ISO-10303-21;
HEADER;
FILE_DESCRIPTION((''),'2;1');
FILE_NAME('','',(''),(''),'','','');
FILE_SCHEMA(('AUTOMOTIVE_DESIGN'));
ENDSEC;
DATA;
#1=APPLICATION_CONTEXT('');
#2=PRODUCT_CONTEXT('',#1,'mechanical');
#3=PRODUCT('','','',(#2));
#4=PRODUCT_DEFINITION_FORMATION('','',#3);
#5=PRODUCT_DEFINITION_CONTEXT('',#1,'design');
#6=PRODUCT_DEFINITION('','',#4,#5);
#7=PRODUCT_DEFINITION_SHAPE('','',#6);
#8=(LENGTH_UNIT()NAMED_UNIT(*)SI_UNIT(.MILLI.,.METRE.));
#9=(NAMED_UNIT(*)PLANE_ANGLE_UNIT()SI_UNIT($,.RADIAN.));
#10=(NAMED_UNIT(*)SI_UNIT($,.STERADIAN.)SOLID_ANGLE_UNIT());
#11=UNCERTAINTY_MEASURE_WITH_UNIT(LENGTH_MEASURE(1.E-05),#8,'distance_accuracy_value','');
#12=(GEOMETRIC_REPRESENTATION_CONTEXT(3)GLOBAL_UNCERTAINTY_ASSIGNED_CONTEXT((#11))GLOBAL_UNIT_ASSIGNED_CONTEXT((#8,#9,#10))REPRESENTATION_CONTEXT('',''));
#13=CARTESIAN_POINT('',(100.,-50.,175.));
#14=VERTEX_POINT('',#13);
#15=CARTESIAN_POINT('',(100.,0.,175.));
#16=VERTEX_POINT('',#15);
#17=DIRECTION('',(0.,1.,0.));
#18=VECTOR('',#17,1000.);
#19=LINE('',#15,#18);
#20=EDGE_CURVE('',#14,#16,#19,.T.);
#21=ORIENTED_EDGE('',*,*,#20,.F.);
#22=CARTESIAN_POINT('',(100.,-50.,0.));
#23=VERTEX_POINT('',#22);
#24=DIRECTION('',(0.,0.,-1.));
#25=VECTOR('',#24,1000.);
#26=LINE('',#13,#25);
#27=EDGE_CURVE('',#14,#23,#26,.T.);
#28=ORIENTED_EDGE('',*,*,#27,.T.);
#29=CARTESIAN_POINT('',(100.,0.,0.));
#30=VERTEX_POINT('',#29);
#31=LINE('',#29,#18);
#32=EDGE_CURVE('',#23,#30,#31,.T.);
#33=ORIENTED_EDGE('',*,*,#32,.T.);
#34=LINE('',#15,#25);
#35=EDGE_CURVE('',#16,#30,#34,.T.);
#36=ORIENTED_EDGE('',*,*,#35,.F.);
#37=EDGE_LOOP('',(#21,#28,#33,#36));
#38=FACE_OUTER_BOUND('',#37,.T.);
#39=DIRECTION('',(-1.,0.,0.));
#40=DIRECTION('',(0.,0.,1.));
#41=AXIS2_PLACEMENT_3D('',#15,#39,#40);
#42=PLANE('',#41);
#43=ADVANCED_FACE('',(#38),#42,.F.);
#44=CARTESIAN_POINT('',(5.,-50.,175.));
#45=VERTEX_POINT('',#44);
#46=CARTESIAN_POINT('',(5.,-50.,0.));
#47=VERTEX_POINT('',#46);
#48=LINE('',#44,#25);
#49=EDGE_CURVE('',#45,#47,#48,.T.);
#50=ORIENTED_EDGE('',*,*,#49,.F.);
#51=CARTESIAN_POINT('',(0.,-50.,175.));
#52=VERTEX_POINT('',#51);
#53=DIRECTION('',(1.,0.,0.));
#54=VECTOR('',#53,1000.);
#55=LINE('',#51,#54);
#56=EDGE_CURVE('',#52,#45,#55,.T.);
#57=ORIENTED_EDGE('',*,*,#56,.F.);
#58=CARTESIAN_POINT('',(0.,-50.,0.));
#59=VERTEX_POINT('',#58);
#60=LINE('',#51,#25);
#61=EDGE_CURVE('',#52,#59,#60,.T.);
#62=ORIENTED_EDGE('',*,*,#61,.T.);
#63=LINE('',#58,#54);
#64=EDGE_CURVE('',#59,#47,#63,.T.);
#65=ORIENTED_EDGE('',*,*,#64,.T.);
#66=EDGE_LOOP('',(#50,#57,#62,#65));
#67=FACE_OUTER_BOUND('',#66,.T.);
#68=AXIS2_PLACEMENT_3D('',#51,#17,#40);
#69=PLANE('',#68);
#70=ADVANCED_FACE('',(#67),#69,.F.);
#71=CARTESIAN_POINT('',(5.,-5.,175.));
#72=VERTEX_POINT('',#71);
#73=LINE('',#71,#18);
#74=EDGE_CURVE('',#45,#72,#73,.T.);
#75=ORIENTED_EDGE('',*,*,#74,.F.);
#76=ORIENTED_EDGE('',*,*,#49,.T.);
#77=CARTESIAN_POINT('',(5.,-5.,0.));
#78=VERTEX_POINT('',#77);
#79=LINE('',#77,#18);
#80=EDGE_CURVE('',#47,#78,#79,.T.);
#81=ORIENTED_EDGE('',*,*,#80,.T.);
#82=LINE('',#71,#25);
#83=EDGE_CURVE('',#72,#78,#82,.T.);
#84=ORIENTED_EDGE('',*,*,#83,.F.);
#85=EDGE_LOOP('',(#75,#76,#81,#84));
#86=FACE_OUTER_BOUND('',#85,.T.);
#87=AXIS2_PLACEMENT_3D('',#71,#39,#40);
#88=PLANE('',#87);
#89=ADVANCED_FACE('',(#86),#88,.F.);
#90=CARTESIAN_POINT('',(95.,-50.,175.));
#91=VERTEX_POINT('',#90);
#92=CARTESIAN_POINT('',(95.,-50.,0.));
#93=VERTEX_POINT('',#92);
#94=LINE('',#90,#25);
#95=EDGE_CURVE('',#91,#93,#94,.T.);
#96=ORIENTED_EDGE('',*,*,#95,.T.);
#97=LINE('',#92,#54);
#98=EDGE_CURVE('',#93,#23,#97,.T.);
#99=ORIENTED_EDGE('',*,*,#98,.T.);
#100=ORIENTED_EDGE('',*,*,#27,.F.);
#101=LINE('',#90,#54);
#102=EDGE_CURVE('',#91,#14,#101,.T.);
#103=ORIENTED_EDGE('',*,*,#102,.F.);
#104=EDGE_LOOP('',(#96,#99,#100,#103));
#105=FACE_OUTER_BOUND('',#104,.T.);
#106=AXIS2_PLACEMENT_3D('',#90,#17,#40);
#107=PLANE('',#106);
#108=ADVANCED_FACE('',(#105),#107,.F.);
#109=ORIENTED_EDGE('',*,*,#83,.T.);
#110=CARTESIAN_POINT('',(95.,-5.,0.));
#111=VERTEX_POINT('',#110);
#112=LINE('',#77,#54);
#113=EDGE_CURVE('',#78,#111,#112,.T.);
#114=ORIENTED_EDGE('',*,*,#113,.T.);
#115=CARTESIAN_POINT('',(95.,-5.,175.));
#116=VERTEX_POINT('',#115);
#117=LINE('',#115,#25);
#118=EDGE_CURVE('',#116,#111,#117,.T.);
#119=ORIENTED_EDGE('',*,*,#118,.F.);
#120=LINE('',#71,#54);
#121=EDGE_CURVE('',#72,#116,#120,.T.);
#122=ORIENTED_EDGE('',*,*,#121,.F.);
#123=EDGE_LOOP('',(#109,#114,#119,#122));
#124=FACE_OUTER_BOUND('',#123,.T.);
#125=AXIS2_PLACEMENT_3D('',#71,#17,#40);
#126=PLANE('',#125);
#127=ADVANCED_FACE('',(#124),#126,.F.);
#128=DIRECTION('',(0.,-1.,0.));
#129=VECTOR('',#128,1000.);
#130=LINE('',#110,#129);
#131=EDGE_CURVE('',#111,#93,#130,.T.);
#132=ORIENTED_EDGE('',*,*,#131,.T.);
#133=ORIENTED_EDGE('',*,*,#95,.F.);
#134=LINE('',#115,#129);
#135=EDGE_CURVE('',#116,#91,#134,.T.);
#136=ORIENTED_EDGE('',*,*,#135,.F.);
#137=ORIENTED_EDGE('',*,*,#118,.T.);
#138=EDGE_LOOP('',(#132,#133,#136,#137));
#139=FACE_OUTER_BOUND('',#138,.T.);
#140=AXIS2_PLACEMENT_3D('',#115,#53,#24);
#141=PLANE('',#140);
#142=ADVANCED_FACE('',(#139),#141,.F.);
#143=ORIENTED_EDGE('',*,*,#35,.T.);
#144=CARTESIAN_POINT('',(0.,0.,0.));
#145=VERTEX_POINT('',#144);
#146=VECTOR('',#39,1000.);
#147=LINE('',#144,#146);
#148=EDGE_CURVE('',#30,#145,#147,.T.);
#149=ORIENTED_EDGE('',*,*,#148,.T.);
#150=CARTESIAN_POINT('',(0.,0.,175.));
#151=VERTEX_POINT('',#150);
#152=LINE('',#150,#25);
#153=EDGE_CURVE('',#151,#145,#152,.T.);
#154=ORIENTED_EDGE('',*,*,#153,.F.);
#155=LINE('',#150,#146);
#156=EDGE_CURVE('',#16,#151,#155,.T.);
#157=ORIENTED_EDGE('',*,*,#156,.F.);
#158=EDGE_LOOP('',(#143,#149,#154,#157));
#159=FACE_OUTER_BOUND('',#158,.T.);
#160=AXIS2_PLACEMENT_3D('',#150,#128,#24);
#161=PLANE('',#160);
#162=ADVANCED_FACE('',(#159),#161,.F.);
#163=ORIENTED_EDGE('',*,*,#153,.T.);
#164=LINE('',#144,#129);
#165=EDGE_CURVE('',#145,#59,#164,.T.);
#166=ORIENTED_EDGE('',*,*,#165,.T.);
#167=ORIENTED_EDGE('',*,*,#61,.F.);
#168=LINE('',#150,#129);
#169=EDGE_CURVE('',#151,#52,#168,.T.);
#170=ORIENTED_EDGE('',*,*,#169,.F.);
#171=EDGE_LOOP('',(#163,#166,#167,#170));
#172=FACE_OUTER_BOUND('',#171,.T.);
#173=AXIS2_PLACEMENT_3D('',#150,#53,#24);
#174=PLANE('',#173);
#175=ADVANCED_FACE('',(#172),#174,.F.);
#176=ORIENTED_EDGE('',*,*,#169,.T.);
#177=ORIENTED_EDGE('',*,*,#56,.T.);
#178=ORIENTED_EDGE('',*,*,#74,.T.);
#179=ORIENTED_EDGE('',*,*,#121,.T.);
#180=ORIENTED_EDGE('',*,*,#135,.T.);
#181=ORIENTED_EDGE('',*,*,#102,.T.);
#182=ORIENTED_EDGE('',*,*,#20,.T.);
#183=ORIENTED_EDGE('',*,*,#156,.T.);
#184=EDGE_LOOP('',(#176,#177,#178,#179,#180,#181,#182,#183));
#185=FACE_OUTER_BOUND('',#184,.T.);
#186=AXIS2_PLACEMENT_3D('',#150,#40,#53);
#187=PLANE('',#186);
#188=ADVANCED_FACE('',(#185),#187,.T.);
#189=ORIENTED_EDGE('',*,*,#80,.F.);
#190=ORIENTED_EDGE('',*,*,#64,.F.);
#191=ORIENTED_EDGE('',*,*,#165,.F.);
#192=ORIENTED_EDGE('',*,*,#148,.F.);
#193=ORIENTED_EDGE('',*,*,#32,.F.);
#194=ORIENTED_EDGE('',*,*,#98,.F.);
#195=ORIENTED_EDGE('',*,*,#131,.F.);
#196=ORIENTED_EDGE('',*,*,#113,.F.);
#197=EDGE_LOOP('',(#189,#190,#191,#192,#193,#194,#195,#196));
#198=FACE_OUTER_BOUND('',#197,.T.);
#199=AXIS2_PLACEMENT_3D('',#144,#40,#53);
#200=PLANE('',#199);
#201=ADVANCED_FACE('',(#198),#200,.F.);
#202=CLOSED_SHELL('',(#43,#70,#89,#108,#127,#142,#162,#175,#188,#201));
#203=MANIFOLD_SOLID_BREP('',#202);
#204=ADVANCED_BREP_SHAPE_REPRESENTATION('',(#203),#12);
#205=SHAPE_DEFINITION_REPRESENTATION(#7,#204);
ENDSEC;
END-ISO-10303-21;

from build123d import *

# Parameters (mm, degrees)
EXTRUDE_1_DEPTH = 175


with BuildPart() as part:
    # 草图1 → 凸台-拉伸1 (new body)
    with BuildSketch(Plane.XY):
        Polygon((0, 0), (100, 0), (100, -50), (95, -50), (95, -5), (5, -5), (5, -50), (0, -50), align=None)
    extrude(amount=EXTRUDE_1_DEPTH)


solid = part.part
